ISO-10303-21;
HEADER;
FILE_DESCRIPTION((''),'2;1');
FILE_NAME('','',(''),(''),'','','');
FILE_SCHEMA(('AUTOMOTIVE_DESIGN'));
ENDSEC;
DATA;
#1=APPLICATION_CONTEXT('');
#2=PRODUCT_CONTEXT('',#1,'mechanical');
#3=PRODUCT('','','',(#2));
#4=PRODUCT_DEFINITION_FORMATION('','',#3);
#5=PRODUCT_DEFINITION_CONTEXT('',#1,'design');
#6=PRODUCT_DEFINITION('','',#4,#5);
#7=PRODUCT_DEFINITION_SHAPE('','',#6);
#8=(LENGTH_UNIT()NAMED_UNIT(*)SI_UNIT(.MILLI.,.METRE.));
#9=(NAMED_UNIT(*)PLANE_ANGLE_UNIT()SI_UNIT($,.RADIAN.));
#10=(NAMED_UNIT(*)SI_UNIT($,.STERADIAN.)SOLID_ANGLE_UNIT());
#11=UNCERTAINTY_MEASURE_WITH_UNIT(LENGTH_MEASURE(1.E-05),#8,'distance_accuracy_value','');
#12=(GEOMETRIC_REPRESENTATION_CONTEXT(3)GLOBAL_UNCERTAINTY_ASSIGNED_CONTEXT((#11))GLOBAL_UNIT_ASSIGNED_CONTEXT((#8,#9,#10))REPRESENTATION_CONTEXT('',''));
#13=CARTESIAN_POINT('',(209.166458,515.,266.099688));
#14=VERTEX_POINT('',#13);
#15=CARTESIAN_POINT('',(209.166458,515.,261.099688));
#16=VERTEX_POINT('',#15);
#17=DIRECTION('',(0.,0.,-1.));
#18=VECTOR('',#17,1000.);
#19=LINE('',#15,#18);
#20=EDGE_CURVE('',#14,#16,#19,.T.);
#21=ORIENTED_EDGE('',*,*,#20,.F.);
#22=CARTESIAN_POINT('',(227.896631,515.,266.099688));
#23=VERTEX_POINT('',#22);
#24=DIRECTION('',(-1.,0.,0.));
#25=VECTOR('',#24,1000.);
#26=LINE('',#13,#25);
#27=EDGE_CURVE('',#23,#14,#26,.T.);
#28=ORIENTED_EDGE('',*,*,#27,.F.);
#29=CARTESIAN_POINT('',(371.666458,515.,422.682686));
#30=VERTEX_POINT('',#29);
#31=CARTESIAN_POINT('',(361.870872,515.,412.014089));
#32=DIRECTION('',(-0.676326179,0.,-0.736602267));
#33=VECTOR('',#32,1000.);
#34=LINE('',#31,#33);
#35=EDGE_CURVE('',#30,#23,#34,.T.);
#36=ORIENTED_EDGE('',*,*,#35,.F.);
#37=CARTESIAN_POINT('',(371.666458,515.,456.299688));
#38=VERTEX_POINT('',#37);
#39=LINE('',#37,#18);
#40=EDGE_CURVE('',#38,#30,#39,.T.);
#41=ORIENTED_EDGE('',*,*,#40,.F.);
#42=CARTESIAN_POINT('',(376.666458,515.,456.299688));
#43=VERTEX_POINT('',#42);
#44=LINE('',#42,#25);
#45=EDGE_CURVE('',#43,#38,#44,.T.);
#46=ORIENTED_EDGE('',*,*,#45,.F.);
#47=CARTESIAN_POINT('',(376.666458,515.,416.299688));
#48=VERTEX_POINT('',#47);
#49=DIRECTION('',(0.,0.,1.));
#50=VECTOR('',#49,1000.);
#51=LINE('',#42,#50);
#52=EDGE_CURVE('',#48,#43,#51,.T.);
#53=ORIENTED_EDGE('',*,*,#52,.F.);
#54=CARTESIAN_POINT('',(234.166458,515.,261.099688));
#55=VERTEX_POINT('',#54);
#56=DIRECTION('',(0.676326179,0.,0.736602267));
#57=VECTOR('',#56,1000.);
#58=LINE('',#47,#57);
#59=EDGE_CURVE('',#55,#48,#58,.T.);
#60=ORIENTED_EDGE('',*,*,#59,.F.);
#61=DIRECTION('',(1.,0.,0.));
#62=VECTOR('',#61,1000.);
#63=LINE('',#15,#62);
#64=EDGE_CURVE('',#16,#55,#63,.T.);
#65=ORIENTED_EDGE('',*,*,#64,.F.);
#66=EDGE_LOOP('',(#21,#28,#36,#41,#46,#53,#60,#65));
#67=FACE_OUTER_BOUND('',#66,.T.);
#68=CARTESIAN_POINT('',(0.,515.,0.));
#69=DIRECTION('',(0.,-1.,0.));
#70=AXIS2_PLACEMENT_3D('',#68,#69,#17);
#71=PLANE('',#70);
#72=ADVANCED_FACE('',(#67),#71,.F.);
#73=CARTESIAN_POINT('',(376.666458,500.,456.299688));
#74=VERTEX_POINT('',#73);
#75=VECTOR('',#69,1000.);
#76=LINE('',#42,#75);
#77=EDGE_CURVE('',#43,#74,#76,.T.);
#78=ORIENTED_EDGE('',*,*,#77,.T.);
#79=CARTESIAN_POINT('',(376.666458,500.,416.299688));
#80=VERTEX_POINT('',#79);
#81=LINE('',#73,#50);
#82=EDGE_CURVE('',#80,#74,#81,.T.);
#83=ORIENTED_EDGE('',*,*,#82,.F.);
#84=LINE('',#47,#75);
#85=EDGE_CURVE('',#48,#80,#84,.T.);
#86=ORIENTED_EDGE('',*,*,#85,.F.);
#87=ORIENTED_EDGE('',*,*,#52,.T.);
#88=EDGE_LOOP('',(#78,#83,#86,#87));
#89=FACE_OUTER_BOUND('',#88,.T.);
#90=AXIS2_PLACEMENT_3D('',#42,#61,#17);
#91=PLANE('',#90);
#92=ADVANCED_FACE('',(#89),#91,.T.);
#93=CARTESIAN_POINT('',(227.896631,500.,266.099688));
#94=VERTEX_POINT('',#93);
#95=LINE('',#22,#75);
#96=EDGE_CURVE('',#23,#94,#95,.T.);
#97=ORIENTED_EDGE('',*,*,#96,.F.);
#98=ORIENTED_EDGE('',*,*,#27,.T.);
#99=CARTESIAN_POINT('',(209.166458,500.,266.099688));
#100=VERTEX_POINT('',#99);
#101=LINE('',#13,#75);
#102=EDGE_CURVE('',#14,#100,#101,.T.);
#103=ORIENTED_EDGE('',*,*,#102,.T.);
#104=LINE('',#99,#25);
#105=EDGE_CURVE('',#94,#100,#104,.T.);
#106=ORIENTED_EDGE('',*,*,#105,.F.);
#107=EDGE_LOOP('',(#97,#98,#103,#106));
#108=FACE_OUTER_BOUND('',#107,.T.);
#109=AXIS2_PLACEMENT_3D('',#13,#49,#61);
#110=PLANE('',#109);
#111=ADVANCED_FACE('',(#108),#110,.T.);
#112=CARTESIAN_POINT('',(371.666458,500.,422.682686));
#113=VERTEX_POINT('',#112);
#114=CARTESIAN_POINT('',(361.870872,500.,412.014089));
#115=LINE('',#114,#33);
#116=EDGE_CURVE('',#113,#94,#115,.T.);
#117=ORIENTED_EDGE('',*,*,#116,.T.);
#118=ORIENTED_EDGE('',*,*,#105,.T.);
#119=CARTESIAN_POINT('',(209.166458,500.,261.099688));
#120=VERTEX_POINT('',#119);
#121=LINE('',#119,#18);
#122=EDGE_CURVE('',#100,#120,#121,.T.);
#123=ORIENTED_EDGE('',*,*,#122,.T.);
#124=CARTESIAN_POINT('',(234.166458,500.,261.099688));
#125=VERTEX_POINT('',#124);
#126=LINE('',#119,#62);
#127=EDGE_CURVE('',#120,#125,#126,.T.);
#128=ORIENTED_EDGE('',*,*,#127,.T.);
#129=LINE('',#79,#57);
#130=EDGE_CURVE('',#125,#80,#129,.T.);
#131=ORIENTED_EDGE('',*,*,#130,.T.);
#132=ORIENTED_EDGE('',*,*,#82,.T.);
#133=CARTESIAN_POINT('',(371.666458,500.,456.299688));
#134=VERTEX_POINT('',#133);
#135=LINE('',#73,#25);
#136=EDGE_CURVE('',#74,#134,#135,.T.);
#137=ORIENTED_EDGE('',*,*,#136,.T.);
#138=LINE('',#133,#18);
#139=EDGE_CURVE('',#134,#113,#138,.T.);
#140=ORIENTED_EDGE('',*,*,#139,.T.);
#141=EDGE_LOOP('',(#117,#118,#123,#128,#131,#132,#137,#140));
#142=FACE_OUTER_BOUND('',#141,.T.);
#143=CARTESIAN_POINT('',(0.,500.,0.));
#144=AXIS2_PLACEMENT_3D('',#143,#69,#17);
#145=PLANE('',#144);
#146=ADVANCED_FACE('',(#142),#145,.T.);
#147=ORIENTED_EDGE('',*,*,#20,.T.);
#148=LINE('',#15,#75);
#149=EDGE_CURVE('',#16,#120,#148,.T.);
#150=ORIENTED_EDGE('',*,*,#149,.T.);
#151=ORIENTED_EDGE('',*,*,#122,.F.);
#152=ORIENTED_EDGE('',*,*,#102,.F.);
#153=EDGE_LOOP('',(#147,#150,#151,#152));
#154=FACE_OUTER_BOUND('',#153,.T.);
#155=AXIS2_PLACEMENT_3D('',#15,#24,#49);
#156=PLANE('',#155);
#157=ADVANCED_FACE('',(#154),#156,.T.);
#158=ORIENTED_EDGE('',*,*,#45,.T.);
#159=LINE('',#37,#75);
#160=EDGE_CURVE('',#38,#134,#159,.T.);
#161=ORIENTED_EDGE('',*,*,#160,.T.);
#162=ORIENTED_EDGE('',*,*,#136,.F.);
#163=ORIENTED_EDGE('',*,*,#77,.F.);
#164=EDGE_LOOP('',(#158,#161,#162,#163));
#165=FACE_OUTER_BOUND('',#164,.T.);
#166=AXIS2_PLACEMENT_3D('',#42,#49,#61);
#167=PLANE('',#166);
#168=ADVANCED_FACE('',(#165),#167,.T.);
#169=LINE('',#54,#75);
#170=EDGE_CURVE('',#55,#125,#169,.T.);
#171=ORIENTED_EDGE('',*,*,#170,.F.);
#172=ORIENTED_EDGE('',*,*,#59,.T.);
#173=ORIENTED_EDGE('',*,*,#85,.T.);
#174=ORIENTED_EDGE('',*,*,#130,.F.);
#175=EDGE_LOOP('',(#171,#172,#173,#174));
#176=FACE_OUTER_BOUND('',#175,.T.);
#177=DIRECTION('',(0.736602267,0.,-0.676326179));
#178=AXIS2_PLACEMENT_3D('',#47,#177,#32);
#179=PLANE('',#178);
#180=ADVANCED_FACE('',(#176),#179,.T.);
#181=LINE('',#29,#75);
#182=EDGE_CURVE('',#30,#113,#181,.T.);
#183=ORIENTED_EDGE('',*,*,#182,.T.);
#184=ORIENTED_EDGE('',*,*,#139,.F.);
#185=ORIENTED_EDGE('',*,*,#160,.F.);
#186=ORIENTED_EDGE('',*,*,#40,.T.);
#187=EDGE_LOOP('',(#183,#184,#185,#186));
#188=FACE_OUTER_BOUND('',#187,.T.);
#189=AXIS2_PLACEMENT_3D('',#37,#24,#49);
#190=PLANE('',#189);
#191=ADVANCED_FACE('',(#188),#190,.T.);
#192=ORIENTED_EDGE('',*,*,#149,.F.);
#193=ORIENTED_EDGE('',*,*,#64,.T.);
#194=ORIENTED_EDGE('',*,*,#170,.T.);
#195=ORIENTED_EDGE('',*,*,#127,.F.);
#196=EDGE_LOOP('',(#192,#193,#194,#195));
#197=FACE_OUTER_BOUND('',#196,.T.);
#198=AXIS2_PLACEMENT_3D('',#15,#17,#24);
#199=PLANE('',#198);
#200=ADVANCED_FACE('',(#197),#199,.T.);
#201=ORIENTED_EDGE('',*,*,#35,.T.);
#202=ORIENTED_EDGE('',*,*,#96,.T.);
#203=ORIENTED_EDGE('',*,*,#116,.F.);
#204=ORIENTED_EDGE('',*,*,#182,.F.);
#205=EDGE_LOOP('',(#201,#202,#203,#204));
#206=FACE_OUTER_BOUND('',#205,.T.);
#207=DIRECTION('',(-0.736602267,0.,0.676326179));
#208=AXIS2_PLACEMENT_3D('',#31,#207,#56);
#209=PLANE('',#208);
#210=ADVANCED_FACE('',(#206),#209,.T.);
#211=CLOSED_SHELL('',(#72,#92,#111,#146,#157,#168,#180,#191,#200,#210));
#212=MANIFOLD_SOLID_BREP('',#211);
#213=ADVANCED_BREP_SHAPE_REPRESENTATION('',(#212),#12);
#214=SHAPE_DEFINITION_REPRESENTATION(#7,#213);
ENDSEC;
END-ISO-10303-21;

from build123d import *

# Parameters (mm, degrees)
BOSS_EXTRUDE1_DEPTH = 15


with BuildPart() as part:
    # Sketch1 → Boss-Extrude1 (new body)
    with BuildSketch(Plane.XZ.offset(-500)):
        Polygon((376.666458359, 456.299687539), (376.666458359, 416.299687539), (234.166458359, 261.099687539), (209.166458359, 261.099687539), (209.166458359, 266.099687539), (227.89663092, 266.099687539), (361.870871539, 412.014088551), (371.666458359, 422.682685565), (371.666458359, 456.299687539), align=None)
    extrude(amount=-BOSS_EXTRUDE1_DEPTH)


solid = part.part
